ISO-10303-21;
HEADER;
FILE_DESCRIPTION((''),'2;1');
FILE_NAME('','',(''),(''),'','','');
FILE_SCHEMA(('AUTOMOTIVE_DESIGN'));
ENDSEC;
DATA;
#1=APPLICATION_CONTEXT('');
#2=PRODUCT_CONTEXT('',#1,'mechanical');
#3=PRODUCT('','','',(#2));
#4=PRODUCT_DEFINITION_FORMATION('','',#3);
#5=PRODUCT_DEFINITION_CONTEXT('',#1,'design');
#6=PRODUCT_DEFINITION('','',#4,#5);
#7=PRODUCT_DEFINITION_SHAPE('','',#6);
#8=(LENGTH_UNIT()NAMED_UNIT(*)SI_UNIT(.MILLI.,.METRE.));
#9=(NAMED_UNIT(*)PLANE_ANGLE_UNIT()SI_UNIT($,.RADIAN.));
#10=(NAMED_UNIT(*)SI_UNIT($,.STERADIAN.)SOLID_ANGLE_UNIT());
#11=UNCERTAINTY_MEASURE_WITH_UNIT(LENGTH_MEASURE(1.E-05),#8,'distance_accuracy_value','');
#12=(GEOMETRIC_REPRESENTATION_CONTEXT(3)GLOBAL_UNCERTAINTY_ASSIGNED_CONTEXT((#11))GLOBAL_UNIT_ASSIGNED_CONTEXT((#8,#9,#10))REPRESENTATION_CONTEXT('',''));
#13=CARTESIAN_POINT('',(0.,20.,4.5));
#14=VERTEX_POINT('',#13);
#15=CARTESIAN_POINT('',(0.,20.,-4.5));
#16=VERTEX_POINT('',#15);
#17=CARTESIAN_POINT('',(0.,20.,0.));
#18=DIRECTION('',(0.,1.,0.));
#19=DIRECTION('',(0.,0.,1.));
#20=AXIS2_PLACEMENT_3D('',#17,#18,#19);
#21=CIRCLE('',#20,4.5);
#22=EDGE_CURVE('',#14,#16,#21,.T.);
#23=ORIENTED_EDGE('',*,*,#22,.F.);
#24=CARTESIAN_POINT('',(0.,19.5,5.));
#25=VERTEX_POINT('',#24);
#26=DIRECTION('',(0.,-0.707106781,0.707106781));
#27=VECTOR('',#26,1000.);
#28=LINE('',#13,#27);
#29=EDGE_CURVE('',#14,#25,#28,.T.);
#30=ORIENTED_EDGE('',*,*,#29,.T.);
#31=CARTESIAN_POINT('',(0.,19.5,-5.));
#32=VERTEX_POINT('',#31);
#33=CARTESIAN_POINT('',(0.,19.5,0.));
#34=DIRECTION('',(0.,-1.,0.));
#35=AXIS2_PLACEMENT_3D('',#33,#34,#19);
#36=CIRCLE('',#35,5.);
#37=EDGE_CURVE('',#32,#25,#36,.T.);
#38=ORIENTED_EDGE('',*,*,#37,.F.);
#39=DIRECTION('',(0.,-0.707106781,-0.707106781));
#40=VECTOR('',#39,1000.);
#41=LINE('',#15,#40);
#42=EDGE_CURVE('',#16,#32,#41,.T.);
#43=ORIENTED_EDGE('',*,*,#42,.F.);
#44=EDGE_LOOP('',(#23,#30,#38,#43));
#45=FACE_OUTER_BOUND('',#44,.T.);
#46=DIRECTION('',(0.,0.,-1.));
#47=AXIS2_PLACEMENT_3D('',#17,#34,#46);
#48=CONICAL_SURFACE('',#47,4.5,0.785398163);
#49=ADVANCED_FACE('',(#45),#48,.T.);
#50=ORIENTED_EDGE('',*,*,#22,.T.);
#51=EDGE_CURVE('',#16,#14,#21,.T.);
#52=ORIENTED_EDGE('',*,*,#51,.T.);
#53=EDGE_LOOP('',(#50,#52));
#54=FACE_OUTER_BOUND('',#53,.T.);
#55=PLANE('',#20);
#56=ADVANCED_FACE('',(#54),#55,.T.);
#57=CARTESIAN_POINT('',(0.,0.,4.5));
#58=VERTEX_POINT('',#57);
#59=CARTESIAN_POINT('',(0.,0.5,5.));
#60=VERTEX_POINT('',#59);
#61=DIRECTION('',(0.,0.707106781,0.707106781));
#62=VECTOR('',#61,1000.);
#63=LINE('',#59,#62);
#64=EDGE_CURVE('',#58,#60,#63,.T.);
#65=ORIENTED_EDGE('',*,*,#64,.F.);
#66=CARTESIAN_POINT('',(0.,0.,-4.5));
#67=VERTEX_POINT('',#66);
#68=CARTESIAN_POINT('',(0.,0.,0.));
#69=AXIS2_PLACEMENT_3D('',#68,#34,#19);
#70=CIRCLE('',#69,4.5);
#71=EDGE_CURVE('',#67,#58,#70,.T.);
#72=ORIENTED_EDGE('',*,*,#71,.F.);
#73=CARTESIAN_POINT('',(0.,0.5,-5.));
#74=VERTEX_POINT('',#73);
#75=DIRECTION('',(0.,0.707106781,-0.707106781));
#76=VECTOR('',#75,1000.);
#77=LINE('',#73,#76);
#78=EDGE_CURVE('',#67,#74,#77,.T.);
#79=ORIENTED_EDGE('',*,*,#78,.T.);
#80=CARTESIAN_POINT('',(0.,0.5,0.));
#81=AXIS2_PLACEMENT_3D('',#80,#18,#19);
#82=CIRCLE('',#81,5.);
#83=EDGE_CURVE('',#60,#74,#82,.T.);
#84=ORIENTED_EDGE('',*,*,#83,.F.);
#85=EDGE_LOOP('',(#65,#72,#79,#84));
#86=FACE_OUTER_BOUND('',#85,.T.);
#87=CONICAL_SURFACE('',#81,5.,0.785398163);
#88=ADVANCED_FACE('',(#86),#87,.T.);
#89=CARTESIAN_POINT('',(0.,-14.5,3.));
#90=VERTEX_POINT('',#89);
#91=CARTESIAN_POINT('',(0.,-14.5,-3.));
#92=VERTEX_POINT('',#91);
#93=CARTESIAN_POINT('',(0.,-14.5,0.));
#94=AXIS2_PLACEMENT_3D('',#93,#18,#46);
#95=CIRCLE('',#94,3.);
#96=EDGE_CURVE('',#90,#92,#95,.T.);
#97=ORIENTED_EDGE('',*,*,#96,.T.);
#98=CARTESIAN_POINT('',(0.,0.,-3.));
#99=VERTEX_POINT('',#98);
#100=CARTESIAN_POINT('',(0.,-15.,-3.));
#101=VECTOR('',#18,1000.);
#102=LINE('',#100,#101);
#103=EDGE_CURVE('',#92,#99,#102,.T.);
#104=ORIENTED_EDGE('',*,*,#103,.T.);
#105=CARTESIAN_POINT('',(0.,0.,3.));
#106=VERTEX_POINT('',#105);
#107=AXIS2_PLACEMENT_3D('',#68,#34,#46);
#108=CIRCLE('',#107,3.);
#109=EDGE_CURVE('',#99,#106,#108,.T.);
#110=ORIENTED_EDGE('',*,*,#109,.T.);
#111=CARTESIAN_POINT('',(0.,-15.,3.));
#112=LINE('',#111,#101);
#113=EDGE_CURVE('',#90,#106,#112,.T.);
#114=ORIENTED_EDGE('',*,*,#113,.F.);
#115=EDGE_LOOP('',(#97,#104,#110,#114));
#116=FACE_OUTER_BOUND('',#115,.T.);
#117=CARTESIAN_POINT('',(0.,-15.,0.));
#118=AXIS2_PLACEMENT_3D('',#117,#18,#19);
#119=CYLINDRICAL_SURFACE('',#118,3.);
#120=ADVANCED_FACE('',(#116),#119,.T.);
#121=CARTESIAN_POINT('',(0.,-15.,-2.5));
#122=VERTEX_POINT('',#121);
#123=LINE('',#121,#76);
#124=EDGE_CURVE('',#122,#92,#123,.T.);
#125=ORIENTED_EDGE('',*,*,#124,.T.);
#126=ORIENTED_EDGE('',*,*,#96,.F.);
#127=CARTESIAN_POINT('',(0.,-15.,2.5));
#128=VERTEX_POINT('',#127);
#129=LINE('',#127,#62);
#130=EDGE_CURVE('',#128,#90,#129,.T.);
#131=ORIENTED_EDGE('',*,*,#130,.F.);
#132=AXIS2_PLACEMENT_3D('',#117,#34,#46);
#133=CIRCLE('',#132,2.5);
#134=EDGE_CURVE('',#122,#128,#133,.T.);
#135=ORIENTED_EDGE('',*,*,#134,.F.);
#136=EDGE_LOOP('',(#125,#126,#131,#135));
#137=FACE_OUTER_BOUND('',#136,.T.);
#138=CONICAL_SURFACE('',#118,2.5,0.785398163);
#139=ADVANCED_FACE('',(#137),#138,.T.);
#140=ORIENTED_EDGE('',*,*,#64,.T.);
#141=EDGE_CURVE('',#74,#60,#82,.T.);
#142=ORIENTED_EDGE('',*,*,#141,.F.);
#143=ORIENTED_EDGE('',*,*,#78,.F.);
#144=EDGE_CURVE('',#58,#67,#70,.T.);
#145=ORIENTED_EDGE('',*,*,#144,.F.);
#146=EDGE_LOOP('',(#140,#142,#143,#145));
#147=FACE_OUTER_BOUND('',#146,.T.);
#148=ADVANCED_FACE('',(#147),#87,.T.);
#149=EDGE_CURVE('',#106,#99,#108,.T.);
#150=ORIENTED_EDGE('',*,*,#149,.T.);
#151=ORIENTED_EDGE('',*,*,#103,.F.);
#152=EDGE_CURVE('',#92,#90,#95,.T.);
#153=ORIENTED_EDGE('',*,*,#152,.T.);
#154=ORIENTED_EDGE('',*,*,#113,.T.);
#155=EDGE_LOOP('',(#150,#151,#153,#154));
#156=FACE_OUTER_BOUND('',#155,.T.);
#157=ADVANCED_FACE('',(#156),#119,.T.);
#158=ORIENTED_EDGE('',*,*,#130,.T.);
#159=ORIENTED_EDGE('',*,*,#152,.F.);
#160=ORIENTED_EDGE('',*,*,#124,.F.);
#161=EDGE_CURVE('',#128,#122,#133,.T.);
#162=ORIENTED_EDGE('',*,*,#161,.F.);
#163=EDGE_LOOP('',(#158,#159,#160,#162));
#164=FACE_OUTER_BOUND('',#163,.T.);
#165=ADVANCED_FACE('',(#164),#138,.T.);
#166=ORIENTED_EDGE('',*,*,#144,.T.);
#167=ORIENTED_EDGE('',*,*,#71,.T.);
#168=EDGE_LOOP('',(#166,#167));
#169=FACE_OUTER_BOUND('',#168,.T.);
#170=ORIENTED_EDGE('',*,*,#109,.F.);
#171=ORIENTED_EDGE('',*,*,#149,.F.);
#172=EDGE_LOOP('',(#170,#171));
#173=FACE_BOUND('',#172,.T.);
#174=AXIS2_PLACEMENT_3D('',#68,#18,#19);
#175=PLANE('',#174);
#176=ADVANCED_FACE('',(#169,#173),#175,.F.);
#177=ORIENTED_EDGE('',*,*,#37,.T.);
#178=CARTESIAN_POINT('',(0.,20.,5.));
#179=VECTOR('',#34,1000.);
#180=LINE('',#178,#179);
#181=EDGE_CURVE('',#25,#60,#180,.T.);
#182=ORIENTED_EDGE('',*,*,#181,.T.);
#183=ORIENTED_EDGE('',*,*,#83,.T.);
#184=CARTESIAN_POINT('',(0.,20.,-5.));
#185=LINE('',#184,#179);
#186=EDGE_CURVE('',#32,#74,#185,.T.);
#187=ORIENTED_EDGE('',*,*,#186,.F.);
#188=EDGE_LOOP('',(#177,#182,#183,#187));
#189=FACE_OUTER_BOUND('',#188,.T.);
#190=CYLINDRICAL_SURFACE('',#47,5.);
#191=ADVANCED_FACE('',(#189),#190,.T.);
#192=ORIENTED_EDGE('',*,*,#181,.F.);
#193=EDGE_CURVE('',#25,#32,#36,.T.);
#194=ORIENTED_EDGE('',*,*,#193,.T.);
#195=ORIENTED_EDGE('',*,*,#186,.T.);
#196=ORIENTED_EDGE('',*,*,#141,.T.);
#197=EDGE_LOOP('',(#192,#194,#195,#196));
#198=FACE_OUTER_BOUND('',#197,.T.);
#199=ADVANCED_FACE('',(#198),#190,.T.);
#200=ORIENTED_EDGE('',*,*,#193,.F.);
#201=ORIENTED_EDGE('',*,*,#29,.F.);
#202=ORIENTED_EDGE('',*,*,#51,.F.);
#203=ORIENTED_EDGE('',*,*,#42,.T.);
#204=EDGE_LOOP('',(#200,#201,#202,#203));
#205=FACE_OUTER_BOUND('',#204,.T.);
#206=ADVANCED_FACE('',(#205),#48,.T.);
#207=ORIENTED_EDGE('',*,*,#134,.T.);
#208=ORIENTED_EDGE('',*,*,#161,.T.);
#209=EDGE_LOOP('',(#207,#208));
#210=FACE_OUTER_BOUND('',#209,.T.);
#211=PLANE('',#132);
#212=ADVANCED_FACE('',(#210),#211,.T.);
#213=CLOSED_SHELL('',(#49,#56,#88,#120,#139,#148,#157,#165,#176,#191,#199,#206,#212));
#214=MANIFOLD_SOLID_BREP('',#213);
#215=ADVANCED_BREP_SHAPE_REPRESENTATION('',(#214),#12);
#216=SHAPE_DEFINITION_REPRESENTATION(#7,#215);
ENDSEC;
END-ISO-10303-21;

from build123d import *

# Parameters (mm, degrees)
SKETCH1_R           = 5
BOSS_EXTRUDE1_DEPTH = 20
SKETCH2_R           = 3
BOSS_EXTRUDE2_DEPTH = 15
CHAMFER1_SIZE       = 0.5


with BuildPart() as part:
    # Sketch1 → Boss-Extrude1 (new body)
    with BuildSketch(Plane(origin=(0, 0, 0), x_dir=(1, 0, 0), z_dir=(0, 1, 0))):
        with Locations(Location((0, 0, 0), (0, 0, 270))):
            Circle(SKETCH1_R)
    extrude(amount=BOSS_EXTRUDE1_DEPTH)

    # Sketch2 → Boss-Extrude2 (add)
    with BuildSketch(Plane.XZ):
        with Locations(Location((0, 0, 0), (0, 0, 270))):
            Circle(SKETCH2_R)
    extrude(amount=BOSS_EXTRUDE2_DEPTH)

    # Chamfer1
    chamfer1_edges = [part.edges().sort_by_distance(p)[0] for p in [
        (0, 0, -5),
        (0, 20, -5),
        (0, -15, 3),
    ]]
    chamfer(chamfer1_edges, length=CHAMFER1_SIZE)


solid = part.part
